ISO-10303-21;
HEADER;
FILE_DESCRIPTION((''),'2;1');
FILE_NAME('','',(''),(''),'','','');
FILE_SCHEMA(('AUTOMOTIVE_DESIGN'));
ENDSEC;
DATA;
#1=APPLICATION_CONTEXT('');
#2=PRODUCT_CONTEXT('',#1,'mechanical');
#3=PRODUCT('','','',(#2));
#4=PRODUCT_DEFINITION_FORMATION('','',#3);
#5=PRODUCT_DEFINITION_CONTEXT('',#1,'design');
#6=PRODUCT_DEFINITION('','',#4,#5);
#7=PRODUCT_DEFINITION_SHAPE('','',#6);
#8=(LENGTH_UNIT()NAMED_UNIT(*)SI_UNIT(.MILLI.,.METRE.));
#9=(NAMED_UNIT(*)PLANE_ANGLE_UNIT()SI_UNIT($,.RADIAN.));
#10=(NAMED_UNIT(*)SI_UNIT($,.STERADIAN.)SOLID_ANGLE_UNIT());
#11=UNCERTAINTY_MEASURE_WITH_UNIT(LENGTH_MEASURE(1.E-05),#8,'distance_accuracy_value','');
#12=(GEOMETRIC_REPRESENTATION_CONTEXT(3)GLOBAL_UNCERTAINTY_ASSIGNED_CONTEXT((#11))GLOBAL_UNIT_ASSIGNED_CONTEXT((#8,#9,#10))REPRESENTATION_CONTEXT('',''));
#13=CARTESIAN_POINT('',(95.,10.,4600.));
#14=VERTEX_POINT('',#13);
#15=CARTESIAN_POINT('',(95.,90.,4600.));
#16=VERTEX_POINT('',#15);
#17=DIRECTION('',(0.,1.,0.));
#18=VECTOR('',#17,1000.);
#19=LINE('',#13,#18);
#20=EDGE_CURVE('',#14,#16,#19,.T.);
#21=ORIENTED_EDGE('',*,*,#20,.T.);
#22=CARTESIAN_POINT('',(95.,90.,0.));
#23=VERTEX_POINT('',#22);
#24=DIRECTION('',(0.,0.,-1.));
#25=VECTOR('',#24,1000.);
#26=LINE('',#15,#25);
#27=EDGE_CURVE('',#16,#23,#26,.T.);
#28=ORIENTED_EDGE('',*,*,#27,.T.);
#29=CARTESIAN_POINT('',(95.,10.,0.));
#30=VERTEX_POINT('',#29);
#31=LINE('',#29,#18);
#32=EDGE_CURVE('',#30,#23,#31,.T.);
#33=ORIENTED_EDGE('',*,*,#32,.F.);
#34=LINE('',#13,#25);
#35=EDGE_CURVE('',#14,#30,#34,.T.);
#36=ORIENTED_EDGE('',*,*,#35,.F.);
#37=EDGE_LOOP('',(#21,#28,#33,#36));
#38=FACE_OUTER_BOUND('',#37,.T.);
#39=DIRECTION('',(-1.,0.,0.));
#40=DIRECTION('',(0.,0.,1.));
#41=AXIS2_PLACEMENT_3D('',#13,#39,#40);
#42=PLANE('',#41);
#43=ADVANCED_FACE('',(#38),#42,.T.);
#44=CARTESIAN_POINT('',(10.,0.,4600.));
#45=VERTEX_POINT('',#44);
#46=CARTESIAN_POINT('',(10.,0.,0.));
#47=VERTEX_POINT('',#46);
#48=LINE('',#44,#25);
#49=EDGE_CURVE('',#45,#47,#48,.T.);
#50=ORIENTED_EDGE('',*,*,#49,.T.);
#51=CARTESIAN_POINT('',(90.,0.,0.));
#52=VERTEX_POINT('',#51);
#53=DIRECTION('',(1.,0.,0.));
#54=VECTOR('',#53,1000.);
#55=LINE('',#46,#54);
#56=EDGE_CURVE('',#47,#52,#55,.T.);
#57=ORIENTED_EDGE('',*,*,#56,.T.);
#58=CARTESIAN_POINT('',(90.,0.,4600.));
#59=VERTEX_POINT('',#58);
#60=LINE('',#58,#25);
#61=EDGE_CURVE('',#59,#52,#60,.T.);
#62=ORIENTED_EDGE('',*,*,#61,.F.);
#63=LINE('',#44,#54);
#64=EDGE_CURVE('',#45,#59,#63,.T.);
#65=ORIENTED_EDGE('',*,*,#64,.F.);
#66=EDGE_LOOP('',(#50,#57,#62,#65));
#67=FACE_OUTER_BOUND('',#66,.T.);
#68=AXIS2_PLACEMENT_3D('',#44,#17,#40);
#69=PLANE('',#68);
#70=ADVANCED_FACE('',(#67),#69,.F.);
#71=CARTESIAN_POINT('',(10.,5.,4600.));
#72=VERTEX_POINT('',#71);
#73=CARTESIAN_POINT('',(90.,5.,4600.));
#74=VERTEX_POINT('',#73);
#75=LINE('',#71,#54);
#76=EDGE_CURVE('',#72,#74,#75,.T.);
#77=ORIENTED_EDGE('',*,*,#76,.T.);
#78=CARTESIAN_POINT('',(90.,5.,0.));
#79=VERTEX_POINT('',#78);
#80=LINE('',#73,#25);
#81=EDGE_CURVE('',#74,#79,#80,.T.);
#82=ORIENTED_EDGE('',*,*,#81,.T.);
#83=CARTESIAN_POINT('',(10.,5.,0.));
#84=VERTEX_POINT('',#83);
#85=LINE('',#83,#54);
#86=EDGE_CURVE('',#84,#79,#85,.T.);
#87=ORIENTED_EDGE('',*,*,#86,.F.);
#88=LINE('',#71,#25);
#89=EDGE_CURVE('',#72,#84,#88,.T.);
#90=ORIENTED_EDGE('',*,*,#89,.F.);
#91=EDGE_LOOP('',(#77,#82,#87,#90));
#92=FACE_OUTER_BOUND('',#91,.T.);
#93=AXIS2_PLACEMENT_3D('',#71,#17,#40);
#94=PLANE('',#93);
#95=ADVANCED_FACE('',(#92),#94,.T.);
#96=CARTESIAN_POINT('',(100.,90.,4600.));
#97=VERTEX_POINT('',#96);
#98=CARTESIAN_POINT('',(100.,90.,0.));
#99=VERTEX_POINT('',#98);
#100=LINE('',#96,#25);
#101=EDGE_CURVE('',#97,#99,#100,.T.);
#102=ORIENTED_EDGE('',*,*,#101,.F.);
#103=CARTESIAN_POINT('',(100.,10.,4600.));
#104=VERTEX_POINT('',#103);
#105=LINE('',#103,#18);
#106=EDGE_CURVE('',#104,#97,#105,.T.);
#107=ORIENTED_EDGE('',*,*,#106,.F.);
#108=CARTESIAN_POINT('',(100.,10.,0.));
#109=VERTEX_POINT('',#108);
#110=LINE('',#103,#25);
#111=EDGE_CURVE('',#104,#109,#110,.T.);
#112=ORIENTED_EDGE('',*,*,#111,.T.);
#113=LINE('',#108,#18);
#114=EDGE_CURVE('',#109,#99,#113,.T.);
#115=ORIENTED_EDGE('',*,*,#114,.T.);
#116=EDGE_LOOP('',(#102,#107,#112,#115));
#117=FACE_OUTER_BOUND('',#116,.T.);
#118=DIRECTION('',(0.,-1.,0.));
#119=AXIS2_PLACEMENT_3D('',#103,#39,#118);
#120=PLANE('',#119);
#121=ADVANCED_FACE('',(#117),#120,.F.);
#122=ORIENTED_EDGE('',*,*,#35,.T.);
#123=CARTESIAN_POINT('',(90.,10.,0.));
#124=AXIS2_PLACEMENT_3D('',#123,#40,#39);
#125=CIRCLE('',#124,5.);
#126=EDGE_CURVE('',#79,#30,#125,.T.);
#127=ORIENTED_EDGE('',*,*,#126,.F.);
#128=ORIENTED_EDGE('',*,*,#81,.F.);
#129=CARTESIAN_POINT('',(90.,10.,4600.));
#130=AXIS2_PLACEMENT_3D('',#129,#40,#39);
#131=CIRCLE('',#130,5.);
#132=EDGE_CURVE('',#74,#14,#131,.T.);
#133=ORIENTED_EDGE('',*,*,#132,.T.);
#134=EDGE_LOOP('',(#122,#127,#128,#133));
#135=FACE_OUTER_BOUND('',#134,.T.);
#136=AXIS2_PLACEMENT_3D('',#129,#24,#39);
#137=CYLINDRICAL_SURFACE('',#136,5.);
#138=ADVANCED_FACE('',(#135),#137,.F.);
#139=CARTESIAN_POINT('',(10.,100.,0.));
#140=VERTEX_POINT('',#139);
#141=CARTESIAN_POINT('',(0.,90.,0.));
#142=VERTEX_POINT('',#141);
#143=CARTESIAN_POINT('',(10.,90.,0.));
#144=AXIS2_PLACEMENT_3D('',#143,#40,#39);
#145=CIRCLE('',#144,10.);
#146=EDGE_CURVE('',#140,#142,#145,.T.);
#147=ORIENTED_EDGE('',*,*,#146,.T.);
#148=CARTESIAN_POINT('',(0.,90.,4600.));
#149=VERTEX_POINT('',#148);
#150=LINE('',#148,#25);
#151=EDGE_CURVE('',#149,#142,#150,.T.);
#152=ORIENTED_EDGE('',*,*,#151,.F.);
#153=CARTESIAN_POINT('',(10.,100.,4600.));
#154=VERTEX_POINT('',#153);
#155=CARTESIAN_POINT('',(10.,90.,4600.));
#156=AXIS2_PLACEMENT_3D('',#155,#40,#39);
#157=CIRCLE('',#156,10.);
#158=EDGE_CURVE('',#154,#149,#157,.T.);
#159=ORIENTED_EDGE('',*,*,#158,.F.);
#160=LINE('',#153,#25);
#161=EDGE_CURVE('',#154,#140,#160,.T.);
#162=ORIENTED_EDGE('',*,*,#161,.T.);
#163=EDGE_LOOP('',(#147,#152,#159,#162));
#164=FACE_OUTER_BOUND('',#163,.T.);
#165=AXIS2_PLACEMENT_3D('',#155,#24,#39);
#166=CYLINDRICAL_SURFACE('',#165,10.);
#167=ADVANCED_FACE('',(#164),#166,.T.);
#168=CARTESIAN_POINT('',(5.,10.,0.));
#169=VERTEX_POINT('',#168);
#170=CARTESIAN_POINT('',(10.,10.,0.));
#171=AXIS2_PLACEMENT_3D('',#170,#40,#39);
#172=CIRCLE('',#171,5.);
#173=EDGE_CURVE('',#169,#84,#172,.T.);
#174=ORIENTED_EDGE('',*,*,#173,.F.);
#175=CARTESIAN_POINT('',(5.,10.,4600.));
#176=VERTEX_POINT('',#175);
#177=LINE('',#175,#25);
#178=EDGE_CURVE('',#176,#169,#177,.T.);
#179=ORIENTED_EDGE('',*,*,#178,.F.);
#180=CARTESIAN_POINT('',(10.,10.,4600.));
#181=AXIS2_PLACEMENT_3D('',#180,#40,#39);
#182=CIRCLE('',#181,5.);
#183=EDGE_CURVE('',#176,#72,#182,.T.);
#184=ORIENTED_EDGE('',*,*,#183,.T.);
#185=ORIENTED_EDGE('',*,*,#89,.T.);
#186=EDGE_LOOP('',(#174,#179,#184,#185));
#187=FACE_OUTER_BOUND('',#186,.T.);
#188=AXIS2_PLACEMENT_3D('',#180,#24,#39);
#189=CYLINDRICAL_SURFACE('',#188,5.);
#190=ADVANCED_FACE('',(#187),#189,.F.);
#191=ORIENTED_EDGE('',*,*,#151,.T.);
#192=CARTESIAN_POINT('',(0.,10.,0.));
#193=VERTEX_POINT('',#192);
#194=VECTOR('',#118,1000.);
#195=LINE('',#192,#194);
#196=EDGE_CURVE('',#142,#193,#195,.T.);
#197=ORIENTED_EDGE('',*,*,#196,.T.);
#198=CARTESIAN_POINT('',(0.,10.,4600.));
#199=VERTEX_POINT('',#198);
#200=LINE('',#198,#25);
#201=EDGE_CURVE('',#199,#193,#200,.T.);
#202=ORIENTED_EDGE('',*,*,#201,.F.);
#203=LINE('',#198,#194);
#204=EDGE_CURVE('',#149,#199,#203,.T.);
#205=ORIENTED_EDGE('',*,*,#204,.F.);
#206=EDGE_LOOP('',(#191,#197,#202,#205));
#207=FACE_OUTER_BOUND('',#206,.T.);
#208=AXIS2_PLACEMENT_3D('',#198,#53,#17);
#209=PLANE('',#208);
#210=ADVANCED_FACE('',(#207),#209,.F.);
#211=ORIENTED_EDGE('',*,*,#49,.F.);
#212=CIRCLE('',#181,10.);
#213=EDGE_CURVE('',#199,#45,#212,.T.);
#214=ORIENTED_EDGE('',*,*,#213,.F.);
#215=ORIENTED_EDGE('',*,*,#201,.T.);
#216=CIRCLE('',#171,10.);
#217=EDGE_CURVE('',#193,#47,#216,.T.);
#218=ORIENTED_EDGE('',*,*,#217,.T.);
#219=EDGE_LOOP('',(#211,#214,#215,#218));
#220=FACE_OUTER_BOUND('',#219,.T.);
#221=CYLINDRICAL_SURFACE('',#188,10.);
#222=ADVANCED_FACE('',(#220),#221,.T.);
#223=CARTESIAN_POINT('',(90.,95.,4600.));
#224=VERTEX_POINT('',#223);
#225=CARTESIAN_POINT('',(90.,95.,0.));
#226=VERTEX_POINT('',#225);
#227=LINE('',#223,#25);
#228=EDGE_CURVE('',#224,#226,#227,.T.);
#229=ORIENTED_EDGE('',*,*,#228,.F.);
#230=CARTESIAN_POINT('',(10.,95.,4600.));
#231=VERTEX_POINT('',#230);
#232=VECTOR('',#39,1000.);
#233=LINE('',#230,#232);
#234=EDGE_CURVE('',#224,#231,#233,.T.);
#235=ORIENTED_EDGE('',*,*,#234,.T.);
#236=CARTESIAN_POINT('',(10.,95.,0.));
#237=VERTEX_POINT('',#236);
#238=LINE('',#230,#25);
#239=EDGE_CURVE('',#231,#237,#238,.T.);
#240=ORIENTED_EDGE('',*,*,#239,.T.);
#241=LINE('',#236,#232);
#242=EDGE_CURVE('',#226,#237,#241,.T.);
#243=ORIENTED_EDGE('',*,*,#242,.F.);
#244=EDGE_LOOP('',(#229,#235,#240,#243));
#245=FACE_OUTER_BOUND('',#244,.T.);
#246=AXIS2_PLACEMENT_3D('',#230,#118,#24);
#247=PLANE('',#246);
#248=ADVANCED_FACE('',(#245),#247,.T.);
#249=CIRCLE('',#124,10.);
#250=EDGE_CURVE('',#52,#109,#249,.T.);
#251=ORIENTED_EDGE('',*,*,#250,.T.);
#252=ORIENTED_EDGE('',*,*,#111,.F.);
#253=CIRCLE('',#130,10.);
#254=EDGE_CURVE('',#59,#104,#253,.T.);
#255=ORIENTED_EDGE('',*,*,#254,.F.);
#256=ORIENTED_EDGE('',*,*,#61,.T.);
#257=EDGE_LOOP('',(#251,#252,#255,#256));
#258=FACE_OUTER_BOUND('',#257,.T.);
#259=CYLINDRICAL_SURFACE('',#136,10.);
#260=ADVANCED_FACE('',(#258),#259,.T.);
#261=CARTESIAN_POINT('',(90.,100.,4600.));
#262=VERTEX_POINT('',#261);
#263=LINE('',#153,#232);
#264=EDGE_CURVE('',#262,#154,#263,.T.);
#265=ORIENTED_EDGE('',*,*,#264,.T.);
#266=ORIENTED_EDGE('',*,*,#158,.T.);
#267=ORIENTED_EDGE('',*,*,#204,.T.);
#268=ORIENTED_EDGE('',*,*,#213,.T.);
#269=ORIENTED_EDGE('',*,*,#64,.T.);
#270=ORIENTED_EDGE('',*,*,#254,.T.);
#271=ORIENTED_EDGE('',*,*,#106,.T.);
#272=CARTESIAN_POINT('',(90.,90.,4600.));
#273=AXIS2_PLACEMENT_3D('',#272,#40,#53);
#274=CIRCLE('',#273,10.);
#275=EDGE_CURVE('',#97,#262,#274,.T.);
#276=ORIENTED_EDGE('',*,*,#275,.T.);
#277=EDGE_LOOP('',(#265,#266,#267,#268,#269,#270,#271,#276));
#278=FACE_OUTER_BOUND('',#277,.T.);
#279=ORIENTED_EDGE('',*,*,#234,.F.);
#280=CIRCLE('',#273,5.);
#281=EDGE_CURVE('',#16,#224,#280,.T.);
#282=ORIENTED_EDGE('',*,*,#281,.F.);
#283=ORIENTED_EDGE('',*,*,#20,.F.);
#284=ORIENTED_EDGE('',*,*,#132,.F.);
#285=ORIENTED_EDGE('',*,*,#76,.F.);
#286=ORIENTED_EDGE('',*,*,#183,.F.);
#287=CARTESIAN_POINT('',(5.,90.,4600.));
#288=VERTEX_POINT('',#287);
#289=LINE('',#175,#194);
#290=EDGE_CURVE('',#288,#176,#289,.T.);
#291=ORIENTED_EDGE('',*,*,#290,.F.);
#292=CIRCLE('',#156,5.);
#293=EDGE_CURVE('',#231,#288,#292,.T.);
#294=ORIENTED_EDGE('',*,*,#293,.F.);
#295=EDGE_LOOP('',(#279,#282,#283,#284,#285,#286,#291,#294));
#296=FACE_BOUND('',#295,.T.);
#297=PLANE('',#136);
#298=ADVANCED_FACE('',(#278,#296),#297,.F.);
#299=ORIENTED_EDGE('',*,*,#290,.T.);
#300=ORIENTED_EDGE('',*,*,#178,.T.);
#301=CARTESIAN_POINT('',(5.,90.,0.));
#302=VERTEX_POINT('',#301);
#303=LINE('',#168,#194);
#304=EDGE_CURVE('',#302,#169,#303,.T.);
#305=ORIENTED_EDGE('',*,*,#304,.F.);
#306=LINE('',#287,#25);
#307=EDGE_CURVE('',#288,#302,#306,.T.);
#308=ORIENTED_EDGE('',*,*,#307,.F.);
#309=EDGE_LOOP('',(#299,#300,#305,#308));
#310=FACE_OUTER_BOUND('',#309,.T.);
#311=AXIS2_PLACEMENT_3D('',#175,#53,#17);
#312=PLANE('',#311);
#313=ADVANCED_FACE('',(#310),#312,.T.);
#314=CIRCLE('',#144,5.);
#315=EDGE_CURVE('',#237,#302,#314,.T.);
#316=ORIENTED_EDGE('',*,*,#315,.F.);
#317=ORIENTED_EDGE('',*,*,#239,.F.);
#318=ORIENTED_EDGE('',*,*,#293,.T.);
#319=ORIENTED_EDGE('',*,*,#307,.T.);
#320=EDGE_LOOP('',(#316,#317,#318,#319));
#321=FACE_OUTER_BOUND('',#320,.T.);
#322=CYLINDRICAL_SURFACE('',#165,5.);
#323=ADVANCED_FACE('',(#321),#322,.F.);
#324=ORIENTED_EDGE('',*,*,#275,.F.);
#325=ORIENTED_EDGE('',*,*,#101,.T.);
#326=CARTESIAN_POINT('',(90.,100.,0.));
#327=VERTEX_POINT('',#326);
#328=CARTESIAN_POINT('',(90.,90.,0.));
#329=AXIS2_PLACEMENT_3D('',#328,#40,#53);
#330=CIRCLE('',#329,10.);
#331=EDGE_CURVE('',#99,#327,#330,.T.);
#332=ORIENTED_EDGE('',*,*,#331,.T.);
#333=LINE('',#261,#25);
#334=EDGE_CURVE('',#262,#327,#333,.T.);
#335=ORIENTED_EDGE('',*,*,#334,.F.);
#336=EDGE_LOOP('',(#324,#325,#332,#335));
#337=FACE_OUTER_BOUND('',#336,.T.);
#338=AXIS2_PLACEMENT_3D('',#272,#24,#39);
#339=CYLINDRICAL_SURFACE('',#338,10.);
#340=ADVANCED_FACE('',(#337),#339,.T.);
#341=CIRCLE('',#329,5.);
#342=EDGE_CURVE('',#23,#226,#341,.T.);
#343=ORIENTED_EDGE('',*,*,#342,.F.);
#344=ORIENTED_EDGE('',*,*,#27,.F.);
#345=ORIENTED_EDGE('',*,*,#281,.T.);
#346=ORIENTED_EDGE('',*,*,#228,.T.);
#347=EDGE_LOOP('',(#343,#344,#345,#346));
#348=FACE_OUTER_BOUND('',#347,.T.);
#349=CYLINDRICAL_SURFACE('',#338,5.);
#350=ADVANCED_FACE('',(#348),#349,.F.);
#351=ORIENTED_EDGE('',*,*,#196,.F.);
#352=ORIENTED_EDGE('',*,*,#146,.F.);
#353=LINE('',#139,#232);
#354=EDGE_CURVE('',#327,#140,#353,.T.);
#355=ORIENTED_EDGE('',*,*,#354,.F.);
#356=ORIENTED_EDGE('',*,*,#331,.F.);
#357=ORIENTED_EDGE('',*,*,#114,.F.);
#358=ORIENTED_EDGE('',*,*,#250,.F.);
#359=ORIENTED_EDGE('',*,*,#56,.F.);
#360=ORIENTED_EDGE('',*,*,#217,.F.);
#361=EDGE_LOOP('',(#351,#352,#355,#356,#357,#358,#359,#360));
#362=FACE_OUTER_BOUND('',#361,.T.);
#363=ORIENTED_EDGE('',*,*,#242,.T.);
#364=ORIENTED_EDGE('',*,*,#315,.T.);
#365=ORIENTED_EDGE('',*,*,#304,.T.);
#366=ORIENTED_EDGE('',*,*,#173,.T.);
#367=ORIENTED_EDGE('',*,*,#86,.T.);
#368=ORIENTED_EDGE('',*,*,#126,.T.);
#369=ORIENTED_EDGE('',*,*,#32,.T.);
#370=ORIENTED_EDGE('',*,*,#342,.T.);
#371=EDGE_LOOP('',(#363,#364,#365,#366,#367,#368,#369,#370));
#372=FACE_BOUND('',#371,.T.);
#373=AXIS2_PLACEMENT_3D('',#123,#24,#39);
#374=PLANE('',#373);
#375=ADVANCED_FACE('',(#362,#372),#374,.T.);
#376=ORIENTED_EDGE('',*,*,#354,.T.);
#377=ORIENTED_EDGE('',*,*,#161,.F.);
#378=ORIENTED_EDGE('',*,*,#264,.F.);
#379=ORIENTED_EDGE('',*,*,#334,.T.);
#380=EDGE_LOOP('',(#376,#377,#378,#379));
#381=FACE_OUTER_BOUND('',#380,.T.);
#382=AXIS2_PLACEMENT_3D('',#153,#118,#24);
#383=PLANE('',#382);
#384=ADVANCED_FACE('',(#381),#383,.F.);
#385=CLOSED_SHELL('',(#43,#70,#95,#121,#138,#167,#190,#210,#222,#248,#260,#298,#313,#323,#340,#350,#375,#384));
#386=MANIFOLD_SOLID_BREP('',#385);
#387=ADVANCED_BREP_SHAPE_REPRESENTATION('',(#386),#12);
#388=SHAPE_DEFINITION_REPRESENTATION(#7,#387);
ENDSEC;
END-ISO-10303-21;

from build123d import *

# Parameters (mm, degrees)
BOSS_EXTRUDE1_DEPTH = 4600


with BuildPart() as part:
    # Sketch1 → Boss-Extrude1 (new body)
    with BuildSketch(Plane.XY):
        with BuildLine():
            Line((10, 0), (90, 0))
            ThreePointArc((90, 0), (97.071067812, 2.928932188), (100, 10))
            Line((100, 10), (100, 90))
            ThreePointArc((100, 90), (97.071067812, 97.071067812), (90, 100))
            Line((90, 100), (10, 100))
            ThreePointArc((10, 100), (2.928932188, 97.071067812), (0, 90))
            Line((0, 90), (0, 10))
            ThreePointArc((0, 10), (2.928932188, 2.928932188), (10, 0))
        make_face()
        with BuildLine():
            Line((10, 95), (90, 95))
            ThreePointArc((90, 95), (93.535533906, 93.535533906), (95, 90))
            Line((95, 90), (95, 10))
            ThreePointArc((95, 10), (93.535533906, 6.464466094), (90, 5))
            Line((90, 5), (10, 5))
            ThreePointArc((10, 5), (6.464466094, 6.464466094), (5, 10))
            Line((5, 10), (5, 90))
            ThreePointArc((5, 90), (6.464466094, 93.535533906), (10, 95))
        make_face(mode=Mode.SUBTRACT)
    extrude(amount=BOSS_EXTRUDE1_DEPTH)


solid = part.part
